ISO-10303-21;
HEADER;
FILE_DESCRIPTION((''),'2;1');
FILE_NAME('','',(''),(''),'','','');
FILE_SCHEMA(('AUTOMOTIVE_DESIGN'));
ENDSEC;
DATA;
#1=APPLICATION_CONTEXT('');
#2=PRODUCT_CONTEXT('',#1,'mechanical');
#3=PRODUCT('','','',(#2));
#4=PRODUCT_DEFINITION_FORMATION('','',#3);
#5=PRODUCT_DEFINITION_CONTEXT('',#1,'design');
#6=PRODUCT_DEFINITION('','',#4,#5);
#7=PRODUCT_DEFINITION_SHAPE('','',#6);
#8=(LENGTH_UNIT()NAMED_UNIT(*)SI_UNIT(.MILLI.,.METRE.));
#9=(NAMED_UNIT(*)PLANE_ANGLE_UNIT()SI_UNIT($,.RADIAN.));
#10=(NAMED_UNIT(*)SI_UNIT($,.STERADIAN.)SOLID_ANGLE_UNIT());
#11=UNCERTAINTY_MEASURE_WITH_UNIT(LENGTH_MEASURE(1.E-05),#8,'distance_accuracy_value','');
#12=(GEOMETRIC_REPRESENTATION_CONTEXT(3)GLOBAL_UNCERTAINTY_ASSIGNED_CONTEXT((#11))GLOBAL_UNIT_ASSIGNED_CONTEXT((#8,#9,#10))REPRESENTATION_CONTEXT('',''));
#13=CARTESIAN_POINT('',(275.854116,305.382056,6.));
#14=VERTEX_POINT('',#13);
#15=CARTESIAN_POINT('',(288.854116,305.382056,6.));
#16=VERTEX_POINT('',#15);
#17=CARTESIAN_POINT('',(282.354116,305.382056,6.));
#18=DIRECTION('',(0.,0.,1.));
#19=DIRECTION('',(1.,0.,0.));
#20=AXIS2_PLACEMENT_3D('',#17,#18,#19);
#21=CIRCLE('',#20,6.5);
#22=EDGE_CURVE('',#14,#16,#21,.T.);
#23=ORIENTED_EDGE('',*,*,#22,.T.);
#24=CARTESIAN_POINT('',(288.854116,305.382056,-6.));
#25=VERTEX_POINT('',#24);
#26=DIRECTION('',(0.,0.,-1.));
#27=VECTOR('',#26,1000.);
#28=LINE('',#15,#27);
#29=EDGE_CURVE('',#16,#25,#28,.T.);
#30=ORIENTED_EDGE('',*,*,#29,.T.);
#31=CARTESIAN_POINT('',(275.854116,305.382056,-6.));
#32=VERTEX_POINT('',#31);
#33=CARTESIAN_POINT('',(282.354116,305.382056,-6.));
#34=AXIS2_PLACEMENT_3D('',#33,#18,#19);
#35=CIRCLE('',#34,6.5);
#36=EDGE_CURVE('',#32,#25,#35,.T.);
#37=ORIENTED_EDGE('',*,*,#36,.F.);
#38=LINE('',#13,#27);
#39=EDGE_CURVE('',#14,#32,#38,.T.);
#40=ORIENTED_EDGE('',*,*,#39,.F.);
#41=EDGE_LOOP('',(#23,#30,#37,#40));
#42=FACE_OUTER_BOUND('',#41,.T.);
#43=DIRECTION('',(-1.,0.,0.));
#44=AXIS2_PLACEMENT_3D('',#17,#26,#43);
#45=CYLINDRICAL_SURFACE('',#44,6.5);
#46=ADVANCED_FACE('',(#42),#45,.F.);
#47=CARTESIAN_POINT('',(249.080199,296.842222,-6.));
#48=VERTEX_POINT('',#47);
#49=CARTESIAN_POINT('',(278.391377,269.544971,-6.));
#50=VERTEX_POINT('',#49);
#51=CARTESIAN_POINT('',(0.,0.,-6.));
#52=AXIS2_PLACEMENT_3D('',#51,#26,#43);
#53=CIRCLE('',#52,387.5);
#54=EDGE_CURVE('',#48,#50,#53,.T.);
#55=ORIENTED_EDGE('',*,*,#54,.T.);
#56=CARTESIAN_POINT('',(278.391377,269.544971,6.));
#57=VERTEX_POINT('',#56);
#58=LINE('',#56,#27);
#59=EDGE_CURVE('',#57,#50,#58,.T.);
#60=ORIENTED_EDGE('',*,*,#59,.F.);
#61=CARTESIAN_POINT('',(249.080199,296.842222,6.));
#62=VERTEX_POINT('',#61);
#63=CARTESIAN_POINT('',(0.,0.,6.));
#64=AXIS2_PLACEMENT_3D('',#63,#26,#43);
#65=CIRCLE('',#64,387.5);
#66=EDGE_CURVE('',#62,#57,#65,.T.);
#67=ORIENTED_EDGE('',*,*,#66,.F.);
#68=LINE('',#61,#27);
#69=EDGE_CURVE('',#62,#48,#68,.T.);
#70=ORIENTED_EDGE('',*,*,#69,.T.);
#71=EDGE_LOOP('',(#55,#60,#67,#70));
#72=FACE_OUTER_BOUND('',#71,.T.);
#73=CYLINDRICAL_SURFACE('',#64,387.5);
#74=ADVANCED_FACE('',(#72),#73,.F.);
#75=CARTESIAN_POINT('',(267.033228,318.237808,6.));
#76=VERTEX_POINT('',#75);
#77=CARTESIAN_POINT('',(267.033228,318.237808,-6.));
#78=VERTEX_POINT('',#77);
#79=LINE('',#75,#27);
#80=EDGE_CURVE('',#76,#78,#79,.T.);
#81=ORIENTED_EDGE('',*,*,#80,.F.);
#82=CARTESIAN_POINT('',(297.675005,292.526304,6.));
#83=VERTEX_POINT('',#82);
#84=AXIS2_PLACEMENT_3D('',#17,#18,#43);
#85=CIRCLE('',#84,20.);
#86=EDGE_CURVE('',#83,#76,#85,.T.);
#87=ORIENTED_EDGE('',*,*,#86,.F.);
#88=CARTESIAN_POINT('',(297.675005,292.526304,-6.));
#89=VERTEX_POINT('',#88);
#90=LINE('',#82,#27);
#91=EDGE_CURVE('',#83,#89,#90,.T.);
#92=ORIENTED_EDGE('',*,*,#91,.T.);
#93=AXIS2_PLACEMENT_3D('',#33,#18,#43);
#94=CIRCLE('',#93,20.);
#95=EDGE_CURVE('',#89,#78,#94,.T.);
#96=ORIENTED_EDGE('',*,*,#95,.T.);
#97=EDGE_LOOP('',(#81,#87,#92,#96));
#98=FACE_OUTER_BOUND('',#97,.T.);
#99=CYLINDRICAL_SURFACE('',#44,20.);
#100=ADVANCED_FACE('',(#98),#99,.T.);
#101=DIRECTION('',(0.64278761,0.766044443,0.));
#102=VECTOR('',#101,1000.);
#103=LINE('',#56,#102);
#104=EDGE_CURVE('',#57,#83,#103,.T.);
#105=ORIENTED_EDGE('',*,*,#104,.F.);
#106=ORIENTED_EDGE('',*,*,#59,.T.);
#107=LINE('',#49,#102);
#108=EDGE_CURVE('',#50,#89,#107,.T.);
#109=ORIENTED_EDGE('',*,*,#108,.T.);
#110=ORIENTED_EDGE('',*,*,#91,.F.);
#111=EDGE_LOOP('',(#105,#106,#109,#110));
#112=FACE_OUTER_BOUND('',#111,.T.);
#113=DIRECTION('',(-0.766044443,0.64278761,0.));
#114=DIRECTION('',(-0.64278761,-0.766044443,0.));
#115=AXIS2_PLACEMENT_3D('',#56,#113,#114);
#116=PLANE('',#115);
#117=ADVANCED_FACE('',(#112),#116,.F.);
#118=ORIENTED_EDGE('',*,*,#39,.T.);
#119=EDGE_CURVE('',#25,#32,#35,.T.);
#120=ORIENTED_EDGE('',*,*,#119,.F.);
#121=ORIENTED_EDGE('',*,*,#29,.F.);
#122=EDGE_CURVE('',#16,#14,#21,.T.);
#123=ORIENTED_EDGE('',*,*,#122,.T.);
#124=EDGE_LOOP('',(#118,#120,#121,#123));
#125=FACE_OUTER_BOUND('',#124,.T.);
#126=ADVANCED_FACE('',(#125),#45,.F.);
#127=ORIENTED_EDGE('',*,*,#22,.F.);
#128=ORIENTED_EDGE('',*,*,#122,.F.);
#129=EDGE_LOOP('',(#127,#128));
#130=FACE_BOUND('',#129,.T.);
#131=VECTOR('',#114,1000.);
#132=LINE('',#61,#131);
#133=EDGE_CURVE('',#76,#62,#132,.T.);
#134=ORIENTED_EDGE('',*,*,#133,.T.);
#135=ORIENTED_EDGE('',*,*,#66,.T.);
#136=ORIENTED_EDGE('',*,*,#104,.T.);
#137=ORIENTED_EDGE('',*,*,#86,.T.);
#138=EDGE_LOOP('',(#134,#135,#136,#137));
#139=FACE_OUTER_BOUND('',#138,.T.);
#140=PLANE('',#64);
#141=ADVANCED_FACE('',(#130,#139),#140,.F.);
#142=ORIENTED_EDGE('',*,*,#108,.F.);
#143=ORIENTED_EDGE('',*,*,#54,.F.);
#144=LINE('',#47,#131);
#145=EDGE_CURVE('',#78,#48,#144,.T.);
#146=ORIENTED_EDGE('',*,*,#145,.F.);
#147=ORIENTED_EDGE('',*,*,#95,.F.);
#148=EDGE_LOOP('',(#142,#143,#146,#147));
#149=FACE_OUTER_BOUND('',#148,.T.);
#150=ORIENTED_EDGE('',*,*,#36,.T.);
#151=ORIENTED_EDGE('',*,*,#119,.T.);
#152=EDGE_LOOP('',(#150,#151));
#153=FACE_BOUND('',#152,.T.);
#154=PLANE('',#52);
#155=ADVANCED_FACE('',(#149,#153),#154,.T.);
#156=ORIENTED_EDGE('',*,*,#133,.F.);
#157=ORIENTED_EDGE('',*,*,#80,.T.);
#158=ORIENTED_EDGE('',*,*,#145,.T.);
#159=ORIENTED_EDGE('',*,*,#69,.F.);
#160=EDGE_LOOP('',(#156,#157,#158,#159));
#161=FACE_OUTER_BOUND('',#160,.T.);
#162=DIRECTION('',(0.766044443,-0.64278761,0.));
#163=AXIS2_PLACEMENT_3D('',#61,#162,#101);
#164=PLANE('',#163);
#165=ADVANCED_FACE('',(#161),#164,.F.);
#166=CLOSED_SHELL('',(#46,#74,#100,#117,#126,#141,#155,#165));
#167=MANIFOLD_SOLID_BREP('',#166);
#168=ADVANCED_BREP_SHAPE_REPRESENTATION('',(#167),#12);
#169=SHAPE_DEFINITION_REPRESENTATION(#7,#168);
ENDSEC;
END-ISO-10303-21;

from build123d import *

# Parameters (mm, degrees)
SKETCH1_R           = 6.499999992
BOSS_EXTRUDE1_DEPTH = 6


with BuildPart() as part:
    # Sketch1 → Boss-Extrude1 (new, symmetric)
    with BuildSketch(Plane.XY):
        with BuildLine():
            Line((249.080198754, 296.842221709), (267.033227589, 318.237808321))
            ThreePointArc((267.033227589, 318.237808321), (295.209868645, 320.702944991), (297.675005315, 292.526303935))
            Line((297.675005315, 292.526303935), (278.391377025, 269.544970642))
            ThreePointArc((278.391377025, 269.544970642), (264.088717655, 283.572564272), (249.080198754, 296.842221709))
        make_face()
        with Locations((282.354116452, 305.382056128)):
            Circle(SKETCH1_R, mode=Mode.SUBTRACT)
    extrude(amount=BOSS_EXTRUDE1_DEPTH, both=True)


solid = part.part
